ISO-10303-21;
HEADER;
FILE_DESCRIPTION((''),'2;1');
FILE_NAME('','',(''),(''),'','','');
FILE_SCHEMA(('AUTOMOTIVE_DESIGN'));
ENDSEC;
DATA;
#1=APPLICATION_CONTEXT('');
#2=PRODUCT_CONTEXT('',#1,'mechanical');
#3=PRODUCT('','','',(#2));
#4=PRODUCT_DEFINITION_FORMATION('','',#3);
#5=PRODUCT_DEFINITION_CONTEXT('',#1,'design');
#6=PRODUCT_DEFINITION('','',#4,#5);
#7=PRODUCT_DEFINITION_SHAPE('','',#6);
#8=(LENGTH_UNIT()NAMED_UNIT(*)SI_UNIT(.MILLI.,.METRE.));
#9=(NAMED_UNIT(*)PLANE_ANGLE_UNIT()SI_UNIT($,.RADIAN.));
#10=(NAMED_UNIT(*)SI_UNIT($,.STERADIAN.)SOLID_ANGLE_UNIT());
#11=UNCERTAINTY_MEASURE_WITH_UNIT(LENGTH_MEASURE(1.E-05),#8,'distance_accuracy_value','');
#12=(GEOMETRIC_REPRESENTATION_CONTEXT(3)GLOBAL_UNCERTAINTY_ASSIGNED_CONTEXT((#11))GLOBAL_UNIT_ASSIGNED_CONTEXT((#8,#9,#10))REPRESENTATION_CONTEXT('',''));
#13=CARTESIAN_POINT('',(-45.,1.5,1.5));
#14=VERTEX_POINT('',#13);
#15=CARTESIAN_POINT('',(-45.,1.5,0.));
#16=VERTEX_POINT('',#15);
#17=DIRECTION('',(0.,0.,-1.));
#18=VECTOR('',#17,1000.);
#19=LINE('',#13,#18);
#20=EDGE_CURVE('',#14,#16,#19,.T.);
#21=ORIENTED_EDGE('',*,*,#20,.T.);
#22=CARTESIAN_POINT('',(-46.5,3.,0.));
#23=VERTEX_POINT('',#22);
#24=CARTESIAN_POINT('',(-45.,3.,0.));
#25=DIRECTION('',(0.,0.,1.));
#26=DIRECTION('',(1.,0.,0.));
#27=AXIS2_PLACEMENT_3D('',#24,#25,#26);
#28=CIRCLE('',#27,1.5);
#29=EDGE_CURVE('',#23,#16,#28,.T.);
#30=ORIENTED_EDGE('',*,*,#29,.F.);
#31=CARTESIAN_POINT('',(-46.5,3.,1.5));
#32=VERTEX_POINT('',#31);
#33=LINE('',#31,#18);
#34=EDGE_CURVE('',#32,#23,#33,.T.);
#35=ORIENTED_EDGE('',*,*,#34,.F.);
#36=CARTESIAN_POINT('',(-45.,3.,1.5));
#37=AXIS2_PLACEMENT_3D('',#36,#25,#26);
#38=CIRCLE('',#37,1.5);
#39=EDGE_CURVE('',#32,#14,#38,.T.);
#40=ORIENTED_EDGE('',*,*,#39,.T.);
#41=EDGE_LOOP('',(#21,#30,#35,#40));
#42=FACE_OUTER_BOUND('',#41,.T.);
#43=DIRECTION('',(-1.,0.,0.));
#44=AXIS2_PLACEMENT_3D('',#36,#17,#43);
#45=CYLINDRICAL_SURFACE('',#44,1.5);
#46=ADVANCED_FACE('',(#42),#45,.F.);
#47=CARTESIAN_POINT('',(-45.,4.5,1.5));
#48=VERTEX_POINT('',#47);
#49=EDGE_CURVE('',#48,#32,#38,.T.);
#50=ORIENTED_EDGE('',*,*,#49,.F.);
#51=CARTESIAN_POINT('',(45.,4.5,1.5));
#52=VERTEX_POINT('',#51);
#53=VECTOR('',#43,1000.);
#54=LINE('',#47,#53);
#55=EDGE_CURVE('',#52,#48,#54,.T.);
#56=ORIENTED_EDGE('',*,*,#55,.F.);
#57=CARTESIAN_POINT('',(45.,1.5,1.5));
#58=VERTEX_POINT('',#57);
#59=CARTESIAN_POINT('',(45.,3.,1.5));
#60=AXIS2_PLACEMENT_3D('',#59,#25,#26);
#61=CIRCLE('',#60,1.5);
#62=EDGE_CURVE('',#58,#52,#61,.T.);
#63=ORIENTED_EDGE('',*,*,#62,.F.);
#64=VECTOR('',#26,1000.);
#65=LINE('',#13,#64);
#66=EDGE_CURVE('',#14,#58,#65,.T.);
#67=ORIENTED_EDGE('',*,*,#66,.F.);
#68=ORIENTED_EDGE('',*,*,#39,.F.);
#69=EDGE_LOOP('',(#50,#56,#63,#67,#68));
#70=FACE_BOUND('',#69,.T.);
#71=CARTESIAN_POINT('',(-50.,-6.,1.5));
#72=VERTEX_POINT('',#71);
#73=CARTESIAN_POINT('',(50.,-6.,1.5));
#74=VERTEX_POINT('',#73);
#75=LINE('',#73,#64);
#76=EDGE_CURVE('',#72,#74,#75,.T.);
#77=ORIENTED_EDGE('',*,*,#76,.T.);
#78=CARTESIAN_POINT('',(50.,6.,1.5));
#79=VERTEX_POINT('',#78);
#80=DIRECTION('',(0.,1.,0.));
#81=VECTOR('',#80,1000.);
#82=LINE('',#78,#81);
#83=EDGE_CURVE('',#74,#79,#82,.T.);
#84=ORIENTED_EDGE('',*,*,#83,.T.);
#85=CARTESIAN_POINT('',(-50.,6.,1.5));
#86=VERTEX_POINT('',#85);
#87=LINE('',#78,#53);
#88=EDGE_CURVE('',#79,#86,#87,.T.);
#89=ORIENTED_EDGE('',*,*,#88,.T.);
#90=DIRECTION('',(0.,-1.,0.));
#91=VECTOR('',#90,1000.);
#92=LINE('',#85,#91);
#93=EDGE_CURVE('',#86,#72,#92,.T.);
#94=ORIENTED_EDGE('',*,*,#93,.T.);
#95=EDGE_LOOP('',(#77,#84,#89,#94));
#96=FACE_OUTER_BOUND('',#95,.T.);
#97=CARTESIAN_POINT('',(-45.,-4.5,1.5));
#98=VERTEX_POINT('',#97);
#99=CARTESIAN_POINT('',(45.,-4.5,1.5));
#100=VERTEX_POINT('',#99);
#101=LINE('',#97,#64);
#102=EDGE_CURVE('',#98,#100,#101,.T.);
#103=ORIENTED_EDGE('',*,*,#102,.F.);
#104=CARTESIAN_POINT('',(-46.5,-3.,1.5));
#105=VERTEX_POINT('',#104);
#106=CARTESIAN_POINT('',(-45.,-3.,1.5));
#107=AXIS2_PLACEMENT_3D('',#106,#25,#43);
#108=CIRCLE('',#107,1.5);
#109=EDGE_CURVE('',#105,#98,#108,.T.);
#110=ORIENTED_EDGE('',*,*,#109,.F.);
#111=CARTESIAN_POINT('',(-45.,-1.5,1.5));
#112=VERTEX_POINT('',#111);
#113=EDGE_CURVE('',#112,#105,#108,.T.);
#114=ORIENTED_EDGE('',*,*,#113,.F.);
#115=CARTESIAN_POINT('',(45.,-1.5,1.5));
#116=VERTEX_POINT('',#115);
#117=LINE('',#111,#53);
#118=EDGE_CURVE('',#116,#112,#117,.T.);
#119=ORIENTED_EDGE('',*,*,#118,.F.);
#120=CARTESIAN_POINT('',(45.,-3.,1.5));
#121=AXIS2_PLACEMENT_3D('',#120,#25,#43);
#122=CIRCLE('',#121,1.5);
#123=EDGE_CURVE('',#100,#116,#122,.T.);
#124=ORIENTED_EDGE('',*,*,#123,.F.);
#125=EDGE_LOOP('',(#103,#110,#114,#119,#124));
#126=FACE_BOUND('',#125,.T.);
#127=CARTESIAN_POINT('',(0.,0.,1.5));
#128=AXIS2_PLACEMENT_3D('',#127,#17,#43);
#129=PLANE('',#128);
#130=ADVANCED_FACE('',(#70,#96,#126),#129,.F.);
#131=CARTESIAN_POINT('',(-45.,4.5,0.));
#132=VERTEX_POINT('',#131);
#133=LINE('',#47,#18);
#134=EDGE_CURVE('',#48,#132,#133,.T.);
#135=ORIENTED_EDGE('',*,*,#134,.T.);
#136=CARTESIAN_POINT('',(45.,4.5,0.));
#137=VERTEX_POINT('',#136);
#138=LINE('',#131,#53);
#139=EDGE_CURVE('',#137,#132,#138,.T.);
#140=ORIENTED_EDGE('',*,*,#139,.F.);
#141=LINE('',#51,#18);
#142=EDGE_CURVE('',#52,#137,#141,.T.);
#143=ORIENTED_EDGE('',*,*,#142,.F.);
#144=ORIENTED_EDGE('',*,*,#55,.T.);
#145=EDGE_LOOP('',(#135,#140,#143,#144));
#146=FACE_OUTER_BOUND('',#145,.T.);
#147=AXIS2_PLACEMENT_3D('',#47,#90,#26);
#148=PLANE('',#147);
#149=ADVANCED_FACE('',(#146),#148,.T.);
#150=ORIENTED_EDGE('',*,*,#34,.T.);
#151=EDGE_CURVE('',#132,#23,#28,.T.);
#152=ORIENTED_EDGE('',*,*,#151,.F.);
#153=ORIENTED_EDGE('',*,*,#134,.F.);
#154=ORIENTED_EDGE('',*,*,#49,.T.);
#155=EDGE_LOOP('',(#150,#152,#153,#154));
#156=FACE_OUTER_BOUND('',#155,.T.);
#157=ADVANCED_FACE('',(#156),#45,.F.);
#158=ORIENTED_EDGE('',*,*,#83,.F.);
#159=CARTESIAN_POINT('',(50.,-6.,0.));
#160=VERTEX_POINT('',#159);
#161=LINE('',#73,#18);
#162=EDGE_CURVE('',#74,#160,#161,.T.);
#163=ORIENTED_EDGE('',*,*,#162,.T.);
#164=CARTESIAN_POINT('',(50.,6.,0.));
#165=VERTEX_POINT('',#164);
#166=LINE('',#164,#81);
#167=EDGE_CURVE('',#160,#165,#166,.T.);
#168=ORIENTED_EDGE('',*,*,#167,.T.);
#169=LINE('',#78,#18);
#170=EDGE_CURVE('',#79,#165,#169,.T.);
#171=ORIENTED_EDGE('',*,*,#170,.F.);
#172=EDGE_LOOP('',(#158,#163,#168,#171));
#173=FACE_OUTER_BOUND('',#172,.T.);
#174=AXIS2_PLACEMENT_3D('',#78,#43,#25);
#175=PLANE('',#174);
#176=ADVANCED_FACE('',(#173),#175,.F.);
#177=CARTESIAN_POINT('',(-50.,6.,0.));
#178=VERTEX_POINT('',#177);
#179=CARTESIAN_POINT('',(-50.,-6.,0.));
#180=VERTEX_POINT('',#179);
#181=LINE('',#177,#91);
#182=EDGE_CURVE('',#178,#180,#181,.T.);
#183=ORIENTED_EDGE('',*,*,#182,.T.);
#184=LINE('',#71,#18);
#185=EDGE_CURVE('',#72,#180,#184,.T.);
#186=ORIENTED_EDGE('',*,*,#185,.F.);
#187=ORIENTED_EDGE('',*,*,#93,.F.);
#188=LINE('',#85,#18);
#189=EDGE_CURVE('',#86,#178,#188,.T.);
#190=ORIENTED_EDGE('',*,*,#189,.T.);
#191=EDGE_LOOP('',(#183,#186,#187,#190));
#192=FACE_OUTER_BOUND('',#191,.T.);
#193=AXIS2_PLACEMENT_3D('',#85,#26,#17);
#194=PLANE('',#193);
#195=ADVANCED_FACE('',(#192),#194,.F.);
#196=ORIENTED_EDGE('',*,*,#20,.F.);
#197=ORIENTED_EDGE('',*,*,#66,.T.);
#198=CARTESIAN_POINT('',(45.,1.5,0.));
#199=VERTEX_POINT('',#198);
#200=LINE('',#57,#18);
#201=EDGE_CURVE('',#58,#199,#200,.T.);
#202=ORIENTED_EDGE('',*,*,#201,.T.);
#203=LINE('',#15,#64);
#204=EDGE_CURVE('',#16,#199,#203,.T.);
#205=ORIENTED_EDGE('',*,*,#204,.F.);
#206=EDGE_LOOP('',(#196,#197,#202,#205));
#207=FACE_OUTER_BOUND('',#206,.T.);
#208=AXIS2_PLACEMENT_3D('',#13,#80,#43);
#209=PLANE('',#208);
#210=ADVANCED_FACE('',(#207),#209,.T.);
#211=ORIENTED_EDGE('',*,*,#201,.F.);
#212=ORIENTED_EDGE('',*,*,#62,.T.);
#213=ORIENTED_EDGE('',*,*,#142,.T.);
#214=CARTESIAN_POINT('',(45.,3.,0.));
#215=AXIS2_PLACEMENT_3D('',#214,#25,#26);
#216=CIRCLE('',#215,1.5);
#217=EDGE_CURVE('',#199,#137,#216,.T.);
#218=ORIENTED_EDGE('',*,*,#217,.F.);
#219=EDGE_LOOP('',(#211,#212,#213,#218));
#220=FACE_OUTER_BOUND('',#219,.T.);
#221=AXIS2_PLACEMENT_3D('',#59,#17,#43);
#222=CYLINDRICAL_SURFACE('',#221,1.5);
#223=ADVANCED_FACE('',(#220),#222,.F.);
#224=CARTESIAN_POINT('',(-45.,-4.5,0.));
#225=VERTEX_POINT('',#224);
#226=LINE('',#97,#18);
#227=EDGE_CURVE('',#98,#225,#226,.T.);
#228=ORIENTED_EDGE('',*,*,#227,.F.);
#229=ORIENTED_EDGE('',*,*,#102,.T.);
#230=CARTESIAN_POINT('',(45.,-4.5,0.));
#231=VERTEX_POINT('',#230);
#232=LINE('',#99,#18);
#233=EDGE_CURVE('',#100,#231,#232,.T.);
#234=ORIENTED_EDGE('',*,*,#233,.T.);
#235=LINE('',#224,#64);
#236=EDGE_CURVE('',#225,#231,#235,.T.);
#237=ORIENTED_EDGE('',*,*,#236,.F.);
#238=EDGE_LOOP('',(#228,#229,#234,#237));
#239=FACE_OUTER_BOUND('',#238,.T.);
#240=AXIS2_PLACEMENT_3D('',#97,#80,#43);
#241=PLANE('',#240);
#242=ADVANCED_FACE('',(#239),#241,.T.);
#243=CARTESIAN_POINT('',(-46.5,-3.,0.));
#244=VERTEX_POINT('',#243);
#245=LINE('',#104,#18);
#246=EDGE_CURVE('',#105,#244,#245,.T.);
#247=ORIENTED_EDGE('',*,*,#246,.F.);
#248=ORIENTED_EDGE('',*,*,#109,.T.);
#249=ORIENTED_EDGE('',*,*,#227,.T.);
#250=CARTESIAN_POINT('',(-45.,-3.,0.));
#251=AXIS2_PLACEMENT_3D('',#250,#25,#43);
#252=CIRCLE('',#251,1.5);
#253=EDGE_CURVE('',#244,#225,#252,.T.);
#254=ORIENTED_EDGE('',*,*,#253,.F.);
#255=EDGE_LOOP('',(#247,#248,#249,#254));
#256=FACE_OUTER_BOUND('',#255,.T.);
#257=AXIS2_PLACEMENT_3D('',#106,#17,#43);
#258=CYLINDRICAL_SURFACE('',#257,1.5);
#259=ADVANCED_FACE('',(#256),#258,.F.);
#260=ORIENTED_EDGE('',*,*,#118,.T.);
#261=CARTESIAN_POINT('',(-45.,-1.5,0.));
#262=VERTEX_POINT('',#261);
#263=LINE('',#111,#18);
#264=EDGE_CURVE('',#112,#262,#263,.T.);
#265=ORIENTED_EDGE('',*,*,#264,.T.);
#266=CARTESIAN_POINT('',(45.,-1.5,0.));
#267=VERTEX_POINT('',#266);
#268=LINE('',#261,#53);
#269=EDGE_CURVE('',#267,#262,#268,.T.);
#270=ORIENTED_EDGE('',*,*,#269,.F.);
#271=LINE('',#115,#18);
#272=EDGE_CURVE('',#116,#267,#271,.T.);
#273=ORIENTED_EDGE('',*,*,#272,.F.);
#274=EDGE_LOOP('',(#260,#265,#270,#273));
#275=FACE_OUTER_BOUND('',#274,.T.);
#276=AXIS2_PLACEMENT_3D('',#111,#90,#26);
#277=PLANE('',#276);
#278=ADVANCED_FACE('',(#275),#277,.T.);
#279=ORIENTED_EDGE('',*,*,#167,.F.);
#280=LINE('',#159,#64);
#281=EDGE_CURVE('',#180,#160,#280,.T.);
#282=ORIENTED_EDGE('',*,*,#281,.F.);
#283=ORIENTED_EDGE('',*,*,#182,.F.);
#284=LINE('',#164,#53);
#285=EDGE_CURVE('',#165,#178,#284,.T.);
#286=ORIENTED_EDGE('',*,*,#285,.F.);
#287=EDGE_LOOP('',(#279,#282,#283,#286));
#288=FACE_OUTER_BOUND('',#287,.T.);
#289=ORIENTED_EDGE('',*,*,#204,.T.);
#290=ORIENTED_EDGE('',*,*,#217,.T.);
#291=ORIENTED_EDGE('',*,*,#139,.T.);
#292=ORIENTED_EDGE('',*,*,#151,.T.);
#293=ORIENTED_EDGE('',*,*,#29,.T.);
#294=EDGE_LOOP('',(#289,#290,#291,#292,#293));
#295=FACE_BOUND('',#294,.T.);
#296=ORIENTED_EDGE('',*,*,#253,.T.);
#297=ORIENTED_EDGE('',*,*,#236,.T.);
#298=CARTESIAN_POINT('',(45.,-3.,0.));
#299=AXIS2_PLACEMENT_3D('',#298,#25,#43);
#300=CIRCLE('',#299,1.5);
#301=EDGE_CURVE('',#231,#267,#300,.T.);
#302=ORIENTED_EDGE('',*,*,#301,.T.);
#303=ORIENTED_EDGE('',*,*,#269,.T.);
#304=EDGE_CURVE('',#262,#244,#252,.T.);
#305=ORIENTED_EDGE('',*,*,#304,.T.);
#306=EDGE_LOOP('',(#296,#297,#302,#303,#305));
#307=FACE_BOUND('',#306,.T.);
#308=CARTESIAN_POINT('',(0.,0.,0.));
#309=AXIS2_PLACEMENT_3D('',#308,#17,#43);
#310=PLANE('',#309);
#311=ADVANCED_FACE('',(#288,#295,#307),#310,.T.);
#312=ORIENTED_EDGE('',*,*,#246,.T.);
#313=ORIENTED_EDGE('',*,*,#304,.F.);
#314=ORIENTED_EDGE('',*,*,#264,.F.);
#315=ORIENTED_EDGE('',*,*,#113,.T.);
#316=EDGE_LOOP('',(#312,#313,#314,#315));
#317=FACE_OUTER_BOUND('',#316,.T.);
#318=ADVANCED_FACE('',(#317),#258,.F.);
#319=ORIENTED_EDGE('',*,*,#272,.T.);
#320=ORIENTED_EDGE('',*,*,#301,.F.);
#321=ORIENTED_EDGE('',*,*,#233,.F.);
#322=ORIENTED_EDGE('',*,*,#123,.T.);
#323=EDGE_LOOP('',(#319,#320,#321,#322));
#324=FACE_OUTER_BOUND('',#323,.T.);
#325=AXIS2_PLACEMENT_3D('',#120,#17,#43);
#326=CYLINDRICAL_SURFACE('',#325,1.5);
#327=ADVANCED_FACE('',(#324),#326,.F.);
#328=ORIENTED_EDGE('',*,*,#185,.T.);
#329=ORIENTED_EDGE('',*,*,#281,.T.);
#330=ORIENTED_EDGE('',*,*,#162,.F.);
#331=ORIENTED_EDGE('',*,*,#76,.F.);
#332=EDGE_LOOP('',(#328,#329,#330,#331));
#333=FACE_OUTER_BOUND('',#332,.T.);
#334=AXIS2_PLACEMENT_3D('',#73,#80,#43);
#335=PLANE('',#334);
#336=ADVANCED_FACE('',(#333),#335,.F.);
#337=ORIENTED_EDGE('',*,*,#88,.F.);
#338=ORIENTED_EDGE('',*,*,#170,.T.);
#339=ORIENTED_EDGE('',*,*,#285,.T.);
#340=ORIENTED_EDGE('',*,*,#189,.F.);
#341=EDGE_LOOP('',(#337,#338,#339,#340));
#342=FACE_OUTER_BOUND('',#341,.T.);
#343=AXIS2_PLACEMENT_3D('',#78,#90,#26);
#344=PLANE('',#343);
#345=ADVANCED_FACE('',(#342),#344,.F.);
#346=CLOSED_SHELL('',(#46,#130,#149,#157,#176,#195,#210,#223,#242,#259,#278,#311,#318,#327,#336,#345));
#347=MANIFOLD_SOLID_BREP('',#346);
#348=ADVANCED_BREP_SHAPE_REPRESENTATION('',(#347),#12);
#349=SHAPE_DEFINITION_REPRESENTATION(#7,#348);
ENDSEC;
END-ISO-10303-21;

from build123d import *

# Parameters (mm, degrees)
SKETCH_1_W      = 100
SKETCH_1_H      = 12
EXTRUDE_1_DEPTH = 1.5


with BuildPart() as part:
    # 草图1 → 凸台-拉伸1 (new body)
    with BuildSketch(Plane.XY):
        Rectangle(SKETCH_1_W, SKETCH_1_H)
        with BuildLine():
            Line((-45, 4.5), (45, 4.5))
            ThreePointArc((45, 4.5), (46.5, 3), (45, 1.5))
            Line((45, 1.5), (-45, 1.5))
            ThreePointArc((-45, 1.5), (-46.5, 3), (-45, 4.5))
        make_face(mode=Mode.SUBTRACT)
        with BuildLine():
            Line((-45, -4.5), (45, -4.5))
            ThreePointArc((45, -4.5), (46.5, -3), (45, -1.5))
            Line((45, -1.5), (-45, -1.5))
            ThreePointArc((-45, -1.5), (-46.5, -3), (-45, -4.5))
        make_face(mode=Mode.SUBTRACT)
    extrude(amount=EXTRUDE_1_DEPTH)


solid = part.part
